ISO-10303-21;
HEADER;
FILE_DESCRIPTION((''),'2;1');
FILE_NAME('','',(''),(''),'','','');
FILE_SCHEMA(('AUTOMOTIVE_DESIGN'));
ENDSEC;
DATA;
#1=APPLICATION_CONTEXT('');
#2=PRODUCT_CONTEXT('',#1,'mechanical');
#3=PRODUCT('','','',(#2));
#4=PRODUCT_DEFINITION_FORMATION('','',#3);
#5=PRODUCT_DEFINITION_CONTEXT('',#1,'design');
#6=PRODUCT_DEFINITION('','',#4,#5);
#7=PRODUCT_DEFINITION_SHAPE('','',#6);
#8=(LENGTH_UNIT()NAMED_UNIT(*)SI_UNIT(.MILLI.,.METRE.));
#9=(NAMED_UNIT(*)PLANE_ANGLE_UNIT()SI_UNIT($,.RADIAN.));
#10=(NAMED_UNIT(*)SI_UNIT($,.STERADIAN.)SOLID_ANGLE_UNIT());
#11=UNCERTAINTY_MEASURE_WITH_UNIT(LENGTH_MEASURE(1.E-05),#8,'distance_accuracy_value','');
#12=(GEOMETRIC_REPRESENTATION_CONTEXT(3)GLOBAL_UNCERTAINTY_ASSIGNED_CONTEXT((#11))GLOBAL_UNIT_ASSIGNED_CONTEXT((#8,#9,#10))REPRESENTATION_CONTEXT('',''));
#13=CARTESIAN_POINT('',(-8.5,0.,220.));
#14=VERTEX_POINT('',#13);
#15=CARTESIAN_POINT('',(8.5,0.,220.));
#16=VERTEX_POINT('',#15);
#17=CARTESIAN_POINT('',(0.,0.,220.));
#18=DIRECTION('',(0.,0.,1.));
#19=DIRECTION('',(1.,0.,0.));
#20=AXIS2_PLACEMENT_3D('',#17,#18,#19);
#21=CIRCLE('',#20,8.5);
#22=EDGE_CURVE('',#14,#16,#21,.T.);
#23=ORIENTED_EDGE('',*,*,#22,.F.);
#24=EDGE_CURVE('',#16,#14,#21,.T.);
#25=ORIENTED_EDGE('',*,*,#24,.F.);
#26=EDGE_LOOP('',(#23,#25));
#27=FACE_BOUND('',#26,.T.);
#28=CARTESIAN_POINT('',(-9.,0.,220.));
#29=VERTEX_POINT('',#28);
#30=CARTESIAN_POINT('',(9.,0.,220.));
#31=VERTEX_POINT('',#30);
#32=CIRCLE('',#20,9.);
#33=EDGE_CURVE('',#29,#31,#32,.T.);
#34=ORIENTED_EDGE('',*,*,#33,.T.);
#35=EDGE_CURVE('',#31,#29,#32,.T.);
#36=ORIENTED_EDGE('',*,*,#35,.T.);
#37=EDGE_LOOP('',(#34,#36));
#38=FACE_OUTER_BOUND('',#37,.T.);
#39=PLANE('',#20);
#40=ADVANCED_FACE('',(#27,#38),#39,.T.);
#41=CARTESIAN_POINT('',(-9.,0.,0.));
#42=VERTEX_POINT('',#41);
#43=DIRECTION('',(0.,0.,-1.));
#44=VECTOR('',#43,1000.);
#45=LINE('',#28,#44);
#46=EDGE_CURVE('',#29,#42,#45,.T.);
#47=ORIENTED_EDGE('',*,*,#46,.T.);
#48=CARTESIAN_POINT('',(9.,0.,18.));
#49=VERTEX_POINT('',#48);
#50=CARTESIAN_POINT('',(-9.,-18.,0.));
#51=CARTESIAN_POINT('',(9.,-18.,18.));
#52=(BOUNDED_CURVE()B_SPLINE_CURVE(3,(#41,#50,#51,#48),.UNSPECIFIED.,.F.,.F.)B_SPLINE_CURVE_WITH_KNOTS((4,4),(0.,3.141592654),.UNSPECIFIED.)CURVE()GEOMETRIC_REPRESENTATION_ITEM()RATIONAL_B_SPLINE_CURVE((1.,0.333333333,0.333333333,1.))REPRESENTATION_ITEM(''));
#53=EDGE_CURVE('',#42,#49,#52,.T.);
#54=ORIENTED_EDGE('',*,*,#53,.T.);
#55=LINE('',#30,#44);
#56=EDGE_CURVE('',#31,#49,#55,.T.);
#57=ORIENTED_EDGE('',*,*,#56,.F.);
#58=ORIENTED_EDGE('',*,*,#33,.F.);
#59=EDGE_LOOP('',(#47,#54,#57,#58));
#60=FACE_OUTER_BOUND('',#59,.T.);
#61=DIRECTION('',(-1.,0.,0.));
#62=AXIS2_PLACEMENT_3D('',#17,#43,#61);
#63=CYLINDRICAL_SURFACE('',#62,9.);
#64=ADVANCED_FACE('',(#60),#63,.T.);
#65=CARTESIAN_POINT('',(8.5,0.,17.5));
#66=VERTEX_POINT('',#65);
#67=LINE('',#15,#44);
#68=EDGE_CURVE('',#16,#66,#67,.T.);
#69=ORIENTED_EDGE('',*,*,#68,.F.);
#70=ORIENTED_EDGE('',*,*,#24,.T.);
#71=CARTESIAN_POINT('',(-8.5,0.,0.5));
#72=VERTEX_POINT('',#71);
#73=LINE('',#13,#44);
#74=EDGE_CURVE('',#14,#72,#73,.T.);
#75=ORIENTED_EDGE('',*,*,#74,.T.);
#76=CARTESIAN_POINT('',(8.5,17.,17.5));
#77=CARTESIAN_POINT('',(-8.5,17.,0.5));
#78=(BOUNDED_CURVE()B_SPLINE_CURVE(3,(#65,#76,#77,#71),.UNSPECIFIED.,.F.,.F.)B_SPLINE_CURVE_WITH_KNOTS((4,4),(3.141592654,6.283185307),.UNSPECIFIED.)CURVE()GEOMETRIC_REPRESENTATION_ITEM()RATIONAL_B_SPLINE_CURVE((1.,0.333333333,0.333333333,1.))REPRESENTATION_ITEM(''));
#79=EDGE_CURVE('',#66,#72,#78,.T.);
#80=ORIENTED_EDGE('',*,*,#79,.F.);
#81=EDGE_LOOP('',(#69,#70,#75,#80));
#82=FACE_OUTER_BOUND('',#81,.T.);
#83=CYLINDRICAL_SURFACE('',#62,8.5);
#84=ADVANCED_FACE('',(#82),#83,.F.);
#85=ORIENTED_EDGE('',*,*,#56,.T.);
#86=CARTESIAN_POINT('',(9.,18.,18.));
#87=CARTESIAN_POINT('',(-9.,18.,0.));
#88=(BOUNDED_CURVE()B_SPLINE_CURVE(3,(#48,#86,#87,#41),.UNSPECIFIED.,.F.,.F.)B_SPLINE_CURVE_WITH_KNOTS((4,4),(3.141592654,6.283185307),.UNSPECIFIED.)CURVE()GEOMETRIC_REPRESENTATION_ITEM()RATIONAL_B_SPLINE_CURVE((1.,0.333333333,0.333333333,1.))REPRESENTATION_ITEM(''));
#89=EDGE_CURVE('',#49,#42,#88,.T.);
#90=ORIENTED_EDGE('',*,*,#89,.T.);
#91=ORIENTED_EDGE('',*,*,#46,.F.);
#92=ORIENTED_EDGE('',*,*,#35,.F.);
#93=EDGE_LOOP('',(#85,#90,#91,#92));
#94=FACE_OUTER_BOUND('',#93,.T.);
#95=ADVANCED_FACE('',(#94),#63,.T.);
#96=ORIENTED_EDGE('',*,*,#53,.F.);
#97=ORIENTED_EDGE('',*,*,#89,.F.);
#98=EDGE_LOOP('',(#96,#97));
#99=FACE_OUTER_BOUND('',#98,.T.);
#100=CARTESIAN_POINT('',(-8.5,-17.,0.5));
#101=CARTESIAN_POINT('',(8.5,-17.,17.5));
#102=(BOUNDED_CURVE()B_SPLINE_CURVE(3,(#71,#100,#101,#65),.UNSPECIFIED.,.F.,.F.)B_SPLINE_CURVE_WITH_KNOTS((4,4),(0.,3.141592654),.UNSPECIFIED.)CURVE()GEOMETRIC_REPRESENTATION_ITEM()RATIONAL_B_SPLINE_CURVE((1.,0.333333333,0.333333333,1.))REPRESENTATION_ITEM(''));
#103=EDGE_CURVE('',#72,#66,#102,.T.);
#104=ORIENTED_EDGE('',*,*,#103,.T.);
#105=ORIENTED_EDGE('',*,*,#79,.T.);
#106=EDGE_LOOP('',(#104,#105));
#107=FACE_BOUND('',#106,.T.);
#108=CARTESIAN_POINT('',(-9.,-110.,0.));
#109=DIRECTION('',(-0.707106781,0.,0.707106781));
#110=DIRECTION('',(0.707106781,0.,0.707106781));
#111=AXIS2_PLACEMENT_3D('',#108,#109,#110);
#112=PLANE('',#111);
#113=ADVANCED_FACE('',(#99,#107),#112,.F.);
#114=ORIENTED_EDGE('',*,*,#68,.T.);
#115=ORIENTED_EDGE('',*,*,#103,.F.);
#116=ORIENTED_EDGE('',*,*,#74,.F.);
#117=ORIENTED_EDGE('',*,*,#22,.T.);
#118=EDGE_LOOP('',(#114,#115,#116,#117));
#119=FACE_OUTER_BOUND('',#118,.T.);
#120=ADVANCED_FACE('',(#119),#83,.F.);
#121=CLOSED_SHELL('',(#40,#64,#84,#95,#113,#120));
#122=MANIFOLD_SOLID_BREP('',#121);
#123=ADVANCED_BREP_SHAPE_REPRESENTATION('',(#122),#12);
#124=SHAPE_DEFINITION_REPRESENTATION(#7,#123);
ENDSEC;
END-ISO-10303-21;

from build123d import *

# Parameters (mm, degrees)
SKETCH1_R           = 9
SKETCH1_R_2         = 8.5
BOSS_EXTRUDE1_DEPTH = 220
CUT_EXTRUDE1_DEPTH  = 110


with BuildPart() as part:
    # Sketch1 → Boss-Extrude1 (new body)
    with BuildSketch(Plane.XY):
        Circle(SKETCH1_R)
        Circle(SKETCH1_R_2, mode=Mode.SUBTRACT)
    extrude(amount=BOSS_EXTRUDE1_DEPTH)

    # Sketch2 → Cut-Extrude1 (cut, symmetric)
    with BuildSketch(Plane(origin=(0, 0, 0), x_dir=(1, 0, 0), z_dir=(0, 1, 0))):
        Polygon((-9, 0), (9, 0), (9, -18), align=None)
    extrude(amount=CUT_EXTRUDE1_DEPTH, both=True, mode=Mode.SUBTRACT)


solid = part.part
